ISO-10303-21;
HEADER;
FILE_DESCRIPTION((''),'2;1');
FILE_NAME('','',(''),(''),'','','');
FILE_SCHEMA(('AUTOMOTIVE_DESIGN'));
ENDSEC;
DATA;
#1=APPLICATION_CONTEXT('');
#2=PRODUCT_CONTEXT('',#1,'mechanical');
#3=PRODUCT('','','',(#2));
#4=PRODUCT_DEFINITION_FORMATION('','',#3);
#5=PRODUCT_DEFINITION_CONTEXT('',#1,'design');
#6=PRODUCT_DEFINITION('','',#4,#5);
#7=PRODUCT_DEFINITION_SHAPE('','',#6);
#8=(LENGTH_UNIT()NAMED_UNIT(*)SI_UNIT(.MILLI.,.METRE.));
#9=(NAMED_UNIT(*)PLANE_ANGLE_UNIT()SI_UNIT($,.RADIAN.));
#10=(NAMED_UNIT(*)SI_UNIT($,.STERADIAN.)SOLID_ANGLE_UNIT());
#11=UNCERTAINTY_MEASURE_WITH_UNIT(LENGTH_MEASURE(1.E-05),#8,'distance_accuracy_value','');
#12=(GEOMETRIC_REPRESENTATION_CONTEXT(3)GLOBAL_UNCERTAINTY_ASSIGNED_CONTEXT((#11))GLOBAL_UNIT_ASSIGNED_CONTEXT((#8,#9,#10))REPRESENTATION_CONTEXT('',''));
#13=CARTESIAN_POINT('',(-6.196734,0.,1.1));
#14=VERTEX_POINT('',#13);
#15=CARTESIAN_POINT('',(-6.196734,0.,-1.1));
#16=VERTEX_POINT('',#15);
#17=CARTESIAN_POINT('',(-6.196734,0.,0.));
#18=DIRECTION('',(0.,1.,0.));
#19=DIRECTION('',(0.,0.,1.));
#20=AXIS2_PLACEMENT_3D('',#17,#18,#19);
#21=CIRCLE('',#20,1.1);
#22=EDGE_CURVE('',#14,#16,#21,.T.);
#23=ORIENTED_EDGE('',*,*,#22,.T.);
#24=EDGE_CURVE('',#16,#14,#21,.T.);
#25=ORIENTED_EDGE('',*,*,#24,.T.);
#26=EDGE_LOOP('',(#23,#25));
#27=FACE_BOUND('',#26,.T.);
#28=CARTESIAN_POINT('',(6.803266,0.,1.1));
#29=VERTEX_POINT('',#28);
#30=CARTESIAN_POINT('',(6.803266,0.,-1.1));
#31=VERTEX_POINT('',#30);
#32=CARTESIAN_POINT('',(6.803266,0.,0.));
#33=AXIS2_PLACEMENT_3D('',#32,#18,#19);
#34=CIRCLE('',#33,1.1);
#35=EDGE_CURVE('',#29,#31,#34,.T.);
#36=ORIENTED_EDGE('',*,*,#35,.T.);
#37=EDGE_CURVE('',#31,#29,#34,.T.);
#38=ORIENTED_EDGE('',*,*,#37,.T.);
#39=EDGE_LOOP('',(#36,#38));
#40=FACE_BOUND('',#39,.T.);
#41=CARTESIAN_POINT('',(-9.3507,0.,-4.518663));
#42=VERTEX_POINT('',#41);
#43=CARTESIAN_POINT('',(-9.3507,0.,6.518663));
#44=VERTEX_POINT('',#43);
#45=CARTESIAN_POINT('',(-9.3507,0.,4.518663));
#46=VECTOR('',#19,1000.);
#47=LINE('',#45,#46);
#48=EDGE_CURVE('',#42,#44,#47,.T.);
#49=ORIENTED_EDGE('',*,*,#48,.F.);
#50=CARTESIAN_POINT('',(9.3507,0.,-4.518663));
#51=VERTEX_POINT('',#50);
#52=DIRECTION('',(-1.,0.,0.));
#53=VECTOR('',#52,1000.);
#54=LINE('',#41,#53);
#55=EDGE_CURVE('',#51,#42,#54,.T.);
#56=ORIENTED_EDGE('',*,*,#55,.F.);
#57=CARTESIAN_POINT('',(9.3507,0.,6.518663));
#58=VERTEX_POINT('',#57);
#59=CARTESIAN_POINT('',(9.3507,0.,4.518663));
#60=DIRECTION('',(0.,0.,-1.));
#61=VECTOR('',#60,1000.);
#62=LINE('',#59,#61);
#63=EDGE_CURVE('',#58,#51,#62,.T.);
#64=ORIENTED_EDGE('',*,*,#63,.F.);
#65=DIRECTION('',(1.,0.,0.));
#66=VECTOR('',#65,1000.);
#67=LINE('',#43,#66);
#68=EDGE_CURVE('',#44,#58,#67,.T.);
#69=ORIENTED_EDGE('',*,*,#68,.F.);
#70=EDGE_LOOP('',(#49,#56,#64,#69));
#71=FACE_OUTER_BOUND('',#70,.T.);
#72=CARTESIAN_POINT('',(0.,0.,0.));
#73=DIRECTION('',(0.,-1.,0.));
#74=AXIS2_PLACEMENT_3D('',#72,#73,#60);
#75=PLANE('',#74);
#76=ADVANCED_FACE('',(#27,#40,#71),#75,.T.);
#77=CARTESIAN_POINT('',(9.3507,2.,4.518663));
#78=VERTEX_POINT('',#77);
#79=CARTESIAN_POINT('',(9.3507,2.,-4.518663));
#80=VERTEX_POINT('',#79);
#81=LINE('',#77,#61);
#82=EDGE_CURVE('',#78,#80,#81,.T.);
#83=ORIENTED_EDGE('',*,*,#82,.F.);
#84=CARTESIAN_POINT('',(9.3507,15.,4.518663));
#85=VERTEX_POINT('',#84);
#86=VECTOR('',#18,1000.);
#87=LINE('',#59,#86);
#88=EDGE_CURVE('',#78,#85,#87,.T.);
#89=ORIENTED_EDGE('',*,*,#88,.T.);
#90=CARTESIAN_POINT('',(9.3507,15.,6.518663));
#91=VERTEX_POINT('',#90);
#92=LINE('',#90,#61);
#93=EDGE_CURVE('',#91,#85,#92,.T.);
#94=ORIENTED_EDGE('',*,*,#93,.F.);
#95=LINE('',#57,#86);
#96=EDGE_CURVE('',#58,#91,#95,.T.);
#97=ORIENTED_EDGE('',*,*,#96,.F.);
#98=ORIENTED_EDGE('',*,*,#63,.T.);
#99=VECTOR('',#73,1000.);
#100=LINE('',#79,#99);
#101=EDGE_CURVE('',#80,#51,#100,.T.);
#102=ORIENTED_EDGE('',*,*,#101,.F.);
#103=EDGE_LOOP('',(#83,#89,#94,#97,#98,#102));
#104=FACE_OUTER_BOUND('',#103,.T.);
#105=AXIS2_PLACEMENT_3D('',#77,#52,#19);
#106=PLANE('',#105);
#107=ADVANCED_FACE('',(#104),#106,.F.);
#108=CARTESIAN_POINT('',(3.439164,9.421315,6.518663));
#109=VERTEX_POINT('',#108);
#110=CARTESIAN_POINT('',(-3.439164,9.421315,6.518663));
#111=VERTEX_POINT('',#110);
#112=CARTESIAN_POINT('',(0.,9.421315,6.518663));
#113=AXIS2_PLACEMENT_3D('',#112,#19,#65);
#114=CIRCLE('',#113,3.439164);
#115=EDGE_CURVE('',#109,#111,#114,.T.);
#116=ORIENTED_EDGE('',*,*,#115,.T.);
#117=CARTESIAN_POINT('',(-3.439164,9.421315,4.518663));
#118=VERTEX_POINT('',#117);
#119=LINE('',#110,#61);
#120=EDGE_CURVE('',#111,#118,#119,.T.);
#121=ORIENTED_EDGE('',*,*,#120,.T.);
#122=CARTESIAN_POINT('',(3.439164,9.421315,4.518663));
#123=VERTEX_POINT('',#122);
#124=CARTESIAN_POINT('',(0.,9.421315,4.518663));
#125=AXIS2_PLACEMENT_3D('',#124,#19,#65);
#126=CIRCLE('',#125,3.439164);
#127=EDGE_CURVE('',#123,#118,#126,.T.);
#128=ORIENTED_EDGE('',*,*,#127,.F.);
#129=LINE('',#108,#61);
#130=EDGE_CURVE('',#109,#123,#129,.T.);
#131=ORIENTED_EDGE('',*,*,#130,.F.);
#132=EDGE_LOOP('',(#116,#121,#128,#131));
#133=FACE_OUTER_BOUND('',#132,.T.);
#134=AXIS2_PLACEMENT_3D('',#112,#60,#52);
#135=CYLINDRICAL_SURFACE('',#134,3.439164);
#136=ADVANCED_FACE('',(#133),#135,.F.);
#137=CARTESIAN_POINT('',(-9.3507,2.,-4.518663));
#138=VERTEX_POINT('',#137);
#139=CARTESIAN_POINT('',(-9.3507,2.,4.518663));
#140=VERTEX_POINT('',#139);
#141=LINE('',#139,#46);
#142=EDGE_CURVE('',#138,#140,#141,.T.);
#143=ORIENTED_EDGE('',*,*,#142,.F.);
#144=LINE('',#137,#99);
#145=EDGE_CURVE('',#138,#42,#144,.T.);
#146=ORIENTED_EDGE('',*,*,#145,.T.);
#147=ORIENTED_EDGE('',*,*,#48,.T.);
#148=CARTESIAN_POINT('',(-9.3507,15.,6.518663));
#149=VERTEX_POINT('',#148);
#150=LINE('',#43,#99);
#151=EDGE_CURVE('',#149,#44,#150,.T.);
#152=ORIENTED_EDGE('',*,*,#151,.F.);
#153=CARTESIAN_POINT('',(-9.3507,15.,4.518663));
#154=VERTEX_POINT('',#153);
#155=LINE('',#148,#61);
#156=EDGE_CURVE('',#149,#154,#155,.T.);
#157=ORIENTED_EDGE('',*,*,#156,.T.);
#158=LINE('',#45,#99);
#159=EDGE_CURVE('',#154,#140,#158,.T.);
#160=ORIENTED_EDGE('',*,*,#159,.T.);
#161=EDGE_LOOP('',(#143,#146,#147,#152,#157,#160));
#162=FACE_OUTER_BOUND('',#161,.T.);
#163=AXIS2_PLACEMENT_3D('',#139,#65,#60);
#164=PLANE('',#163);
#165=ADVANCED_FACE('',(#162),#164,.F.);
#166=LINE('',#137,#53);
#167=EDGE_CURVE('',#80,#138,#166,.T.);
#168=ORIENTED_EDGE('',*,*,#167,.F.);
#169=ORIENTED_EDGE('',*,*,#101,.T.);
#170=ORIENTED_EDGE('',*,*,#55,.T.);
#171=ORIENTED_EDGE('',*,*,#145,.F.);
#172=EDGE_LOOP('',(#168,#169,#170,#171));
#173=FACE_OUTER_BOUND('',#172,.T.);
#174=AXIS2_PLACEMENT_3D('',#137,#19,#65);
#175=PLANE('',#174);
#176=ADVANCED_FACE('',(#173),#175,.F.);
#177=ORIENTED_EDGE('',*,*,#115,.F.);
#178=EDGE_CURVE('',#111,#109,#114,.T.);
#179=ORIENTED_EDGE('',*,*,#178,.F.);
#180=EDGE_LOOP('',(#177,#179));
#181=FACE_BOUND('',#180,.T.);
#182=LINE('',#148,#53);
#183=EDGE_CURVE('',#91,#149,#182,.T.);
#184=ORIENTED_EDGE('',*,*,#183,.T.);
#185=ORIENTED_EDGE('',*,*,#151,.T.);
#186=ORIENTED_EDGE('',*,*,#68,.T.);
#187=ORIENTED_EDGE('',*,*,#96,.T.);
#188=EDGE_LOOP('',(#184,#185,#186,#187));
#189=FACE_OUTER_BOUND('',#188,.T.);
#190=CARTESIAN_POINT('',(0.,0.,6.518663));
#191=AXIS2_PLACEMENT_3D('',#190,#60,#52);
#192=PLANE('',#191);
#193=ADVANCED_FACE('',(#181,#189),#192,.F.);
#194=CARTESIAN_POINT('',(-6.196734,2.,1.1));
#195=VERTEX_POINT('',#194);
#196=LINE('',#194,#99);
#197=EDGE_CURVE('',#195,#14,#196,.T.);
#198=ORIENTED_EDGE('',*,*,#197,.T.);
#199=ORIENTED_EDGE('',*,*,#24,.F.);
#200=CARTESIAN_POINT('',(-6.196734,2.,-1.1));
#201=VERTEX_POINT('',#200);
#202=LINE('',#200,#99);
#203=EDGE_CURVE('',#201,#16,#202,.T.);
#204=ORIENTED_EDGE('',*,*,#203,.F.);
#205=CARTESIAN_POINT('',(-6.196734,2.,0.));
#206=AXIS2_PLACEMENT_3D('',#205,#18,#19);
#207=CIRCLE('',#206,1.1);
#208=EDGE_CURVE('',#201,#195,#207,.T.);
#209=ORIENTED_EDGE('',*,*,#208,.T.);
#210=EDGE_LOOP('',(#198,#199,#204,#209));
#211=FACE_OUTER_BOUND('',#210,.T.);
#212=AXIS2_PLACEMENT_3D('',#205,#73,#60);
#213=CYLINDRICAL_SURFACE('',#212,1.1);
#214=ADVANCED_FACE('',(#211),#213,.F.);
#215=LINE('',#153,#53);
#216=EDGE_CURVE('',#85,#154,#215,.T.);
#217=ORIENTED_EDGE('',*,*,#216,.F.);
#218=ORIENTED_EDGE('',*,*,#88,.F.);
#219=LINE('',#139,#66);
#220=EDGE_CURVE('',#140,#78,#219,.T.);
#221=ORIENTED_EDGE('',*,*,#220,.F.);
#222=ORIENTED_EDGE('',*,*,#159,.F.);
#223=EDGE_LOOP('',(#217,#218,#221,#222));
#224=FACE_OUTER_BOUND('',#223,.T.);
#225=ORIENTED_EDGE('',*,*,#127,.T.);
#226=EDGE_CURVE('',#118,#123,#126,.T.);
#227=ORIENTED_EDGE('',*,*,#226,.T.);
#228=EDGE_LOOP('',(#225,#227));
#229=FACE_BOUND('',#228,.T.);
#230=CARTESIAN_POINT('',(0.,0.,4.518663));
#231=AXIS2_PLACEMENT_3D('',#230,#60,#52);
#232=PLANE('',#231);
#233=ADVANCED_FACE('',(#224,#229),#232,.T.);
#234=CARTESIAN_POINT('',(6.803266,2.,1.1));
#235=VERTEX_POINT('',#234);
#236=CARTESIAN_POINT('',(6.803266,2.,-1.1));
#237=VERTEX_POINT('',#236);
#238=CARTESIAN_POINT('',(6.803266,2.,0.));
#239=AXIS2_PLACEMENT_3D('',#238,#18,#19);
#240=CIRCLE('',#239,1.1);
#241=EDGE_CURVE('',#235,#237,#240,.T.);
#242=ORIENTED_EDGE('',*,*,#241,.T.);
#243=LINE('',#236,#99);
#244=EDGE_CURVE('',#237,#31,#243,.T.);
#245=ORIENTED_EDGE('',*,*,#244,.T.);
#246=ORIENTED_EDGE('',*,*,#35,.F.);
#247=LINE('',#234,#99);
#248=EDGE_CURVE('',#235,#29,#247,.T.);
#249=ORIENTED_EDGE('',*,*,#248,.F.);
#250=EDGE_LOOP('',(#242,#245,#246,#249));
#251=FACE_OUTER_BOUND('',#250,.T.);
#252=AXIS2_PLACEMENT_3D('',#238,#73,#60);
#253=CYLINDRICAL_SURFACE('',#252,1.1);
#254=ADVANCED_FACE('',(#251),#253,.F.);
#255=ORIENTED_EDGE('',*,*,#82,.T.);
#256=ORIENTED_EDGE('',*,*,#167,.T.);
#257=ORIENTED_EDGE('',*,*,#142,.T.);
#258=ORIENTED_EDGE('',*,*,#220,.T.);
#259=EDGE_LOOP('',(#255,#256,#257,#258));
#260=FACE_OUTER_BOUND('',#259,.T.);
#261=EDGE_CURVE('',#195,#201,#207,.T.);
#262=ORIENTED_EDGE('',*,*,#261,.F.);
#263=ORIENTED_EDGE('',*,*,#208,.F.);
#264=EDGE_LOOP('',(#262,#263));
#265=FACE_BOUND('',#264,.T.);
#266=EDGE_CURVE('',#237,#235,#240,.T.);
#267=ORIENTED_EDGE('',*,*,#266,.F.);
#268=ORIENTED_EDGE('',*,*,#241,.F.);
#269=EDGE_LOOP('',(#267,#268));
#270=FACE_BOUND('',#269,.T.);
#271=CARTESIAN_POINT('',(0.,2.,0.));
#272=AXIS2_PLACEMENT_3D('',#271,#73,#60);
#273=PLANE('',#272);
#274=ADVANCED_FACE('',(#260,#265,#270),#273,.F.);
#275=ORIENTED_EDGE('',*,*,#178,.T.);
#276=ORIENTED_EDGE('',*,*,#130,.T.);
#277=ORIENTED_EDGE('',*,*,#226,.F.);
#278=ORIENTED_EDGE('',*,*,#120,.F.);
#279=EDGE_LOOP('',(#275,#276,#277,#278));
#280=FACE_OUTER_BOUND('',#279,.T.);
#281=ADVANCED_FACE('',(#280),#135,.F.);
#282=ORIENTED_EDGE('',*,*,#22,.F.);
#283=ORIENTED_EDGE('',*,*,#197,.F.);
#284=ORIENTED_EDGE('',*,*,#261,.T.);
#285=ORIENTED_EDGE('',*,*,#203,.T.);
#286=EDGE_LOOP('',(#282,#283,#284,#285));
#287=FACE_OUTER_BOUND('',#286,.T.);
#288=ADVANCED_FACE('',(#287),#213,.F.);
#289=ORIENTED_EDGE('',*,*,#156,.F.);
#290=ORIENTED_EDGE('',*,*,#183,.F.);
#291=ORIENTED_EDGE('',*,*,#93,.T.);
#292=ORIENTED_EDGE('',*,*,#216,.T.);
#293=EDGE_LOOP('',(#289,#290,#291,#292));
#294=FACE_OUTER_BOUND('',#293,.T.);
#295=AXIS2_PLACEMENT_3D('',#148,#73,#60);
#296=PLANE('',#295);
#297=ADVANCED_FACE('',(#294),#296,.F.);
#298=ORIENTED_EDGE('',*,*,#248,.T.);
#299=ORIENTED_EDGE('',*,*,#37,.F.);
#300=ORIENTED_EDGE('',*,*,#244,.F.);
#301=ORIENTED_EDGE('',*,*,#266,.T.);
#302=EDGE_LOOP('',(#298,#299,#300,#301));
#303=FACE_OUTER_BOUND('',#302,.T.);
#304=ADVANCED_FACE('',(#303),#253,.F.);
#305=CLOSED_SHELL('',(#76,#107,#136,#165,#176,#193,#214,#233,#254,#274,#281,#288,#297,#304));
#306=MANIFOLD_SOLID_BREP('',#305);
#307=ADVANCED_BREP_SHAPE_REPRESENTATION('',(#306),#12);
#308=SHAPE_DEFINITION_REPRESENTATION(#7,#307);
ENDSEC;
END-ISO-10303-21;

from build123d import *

# Parameters (mm, degrees)
SKETCH1_W           = 18.701399688
SKETCH1_H           = 9.037325038
SKETCH1_R           = 1.1
BOSS_EXTRUDE1_DEPTH = 2
SKETCH2_W           = 18.701399688
SKETCH2_H           = 15
SKETCH2_R           = 3.439163943
BOSS_EXTRUDE2_DEPTH = 2


with BuildPart() as part:
    # Sketch1 → Boss-Extrude1 (new body)
    with BuildSketch(Plane(origin=(0, 0, 0), x_dir=(1, 0, 0), z_dir=(0, 1, 0))):
        Rectangle(SKETCH1_W, SKETCH1_H)
        with Locations(Location((-6.196734059, 0, 0), (0, 0, 270))):
            Circle(SKETCH1_R, mode=Mode.SUBTRACT)
        with Locations(Location((6.803265941, 0, 0), (0, 0, 270))):
            Circle(SKETCH1_R, mode=Mode.SUBTRACT)
    extrude(amount=BOSS_EXTRUDE1_DEPTH)

    # Sketch2 → Boss-Extrude2 (add)
    with BuildSketch(Plane.XY.offset(4.518662519)):
        with Locations((0, 7.5)):
            Rectangle(SKETCH2_W, SKETCH2_H)
        with Locations((0, 9.421314685)):
            Circle(SKETCH2_R, mode=Mode.SUBTRACT)
    extrude(amount=BOSS_EXTRUDE2_DEPTH)


solid = part.part
